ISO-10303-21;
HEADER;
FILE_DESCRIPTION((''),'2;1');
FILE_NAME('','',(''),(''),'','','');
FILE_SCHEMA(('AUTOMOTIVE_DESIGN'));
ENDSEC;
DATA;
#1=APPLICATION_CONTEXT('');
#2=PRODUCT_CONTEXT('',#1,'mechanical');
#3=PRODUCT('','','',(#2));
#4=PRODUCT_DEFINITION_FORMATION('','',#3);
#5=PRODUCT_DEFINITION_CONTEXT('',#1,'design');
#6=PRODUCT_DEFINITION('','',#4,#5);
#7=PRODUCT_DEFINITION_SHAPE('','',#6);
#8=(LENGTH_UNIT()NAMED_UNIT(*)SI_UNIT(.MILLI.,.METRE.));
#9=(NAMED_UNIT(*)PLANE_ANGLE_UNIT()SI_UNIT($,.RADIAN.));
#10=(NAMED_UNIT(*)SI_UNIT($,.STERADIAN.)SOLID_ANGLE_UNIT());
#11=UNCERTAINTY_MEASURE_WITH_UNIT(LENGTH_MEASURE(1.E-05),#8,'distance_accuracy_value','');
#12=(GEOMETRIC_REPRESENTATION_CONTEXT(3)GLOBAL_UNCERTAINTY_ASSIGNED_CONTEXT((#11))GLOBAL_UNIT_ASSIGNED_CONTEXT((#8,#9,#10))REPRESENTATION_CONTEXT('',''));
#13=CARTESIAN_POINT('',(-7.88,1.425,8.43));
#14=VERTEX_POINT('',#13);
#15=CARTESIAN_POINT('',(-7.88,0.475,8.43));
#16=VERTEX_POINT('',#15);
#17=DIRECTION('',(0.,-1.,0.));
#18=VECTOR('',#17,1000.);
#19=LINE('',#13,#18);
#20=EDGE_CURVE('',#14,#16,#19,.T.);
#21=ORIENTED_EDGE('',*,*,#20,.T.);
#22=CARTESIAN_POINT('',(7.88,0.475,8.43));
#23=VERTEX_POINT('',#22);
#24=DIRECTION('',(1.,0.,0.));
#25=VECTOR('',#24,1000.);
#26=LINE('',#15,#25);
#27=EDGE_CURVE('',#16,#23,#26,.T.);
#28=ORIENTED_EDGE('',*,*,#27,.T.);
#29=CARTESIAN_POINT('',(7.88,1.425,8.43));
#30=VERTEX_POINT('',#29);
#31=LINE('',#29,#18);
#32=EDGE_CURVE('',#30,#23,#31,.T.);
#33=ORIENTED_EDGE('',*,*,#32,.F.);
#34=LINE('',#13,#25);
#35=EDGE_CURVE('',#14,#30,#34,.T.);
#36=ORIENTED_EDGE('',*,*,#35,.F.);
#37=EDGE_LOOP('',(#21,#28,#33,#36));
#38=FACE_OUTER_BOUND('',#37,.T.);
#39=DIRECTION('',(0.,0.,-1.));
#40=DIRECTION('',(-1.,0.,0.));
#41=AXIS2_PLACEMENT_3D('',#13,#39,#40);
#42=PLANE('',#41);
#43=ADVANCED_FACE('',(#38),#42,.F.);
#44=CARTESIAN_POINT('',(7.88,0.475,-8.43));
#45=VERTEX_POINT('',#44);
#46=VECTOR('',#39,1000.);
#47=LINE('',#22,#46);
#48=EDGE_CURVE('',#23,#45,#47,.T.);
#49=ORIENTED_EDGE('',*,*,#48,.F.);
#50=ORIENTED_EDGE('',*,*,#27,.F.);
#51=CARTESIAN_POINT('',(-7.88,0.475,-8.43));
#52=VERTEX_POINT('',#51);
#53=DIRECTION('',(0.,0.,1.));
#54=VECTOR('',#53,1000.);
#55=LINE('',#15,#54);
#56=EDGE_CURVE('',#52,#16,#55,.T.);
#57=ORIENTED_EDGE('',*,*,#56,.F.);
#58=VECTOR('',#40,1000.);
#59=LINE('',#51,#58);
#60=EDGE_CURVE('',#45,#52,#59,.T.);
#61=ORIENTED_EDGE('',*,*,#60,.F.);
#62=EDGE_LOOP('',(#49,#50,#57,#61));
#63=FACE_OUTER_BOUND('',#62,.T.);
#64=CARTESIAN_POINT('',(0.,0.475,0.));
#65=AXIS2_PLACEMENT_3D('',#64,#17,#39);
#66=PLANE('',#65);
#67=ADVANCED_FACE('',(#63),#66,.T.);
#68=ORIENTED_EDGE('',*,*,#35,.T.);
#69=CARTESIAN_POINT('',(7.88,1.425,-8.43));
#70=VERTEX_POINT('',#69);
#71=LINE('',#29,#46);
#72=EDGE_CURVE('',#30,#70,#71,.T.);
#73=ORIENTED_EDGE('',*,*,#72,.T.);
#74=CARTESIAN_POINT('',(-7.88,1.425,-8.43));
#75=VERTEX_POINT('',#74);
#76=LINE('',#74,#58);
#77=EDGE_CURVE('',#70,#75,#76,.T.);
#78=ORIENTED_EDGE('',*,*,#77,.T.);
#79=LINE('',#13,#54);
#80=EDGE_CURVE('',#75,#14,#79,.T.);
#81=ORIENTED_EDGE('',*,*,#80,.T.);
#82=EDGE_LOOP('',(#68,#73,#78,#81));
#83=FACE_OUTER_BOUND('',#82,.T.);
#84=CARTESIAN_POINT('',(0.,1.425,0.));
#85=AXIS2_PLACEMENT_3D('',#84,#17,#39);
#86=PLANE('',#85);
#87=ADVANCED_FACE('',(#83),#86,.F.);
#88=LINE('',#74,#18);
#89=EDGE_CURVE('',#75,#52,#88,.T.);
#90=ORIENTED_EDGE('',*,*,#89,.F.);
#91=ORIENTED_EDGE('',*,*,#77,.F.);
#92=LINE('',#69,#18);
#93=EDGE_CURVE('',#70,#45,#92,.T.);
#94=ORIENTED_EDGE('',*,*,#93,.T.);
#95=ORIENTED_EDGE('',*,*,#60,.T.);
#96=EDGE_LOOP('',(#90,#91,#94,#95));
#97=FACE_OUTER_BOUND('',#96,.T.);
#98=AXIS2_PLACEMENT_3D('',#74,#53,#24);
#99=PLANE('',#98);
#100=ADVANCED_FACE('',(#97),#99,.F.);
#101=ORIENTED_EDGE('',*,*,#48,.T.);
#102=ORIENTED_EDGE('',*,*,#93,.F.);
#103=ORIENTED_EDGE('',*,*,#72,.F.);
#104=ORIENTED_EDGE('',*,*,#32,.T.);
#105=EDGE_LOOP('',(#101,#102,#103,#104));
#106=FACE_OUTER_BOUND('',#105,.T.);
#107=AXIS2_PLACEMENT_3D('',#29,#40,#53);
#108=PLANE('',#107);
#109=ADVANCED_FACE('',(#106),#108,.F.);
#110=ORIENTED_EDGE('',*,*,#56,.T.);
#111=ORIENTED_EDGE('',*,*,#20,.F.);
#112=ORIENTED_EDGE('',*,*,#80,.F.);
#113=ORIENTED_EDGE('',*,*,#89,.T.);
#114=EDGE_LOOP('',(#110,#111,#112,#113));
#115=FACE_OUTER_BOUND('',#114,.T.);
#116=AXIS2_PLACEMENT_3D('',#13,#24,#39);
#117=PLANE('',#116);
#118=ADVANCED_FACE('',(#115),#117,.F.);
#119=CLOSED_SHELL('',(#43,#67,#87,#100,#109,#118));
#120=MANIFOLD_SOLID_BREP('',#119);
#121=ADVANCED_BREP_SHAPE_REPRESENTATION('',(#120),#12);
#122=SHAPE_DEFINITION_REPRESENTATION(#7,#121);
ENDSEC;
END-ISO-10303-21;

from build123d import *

# Parameters (mm, degrees)
SKETCH1_W           = 31.52
SKETCH1_H           = 33.72
BOSS_EXTRUDE1_DEPTH = 1.9
SCALE1_SCALE        = 0.5


with BuildPart() as part:
    # Sketch1 → Boss-Extrude1 (new body)
    with BuildSketch(Plane(origin=(0, 0, 0), x_dir=(1, 0, 0), z_dir=(0, 1, 0))):
        Rectangle(SKETCH1_W, SKETCH1_H)
    extrude(amount=BOSS_EXTRUDE1_DEPTH)


with BuildPart() as part_1:
    # Scale1: scaled about (0, 0.95, 0)
    add(part.part.scale(SCALE1_SCALE).moved(Location((0, 0.475, 0))))


solid = part_1.part
